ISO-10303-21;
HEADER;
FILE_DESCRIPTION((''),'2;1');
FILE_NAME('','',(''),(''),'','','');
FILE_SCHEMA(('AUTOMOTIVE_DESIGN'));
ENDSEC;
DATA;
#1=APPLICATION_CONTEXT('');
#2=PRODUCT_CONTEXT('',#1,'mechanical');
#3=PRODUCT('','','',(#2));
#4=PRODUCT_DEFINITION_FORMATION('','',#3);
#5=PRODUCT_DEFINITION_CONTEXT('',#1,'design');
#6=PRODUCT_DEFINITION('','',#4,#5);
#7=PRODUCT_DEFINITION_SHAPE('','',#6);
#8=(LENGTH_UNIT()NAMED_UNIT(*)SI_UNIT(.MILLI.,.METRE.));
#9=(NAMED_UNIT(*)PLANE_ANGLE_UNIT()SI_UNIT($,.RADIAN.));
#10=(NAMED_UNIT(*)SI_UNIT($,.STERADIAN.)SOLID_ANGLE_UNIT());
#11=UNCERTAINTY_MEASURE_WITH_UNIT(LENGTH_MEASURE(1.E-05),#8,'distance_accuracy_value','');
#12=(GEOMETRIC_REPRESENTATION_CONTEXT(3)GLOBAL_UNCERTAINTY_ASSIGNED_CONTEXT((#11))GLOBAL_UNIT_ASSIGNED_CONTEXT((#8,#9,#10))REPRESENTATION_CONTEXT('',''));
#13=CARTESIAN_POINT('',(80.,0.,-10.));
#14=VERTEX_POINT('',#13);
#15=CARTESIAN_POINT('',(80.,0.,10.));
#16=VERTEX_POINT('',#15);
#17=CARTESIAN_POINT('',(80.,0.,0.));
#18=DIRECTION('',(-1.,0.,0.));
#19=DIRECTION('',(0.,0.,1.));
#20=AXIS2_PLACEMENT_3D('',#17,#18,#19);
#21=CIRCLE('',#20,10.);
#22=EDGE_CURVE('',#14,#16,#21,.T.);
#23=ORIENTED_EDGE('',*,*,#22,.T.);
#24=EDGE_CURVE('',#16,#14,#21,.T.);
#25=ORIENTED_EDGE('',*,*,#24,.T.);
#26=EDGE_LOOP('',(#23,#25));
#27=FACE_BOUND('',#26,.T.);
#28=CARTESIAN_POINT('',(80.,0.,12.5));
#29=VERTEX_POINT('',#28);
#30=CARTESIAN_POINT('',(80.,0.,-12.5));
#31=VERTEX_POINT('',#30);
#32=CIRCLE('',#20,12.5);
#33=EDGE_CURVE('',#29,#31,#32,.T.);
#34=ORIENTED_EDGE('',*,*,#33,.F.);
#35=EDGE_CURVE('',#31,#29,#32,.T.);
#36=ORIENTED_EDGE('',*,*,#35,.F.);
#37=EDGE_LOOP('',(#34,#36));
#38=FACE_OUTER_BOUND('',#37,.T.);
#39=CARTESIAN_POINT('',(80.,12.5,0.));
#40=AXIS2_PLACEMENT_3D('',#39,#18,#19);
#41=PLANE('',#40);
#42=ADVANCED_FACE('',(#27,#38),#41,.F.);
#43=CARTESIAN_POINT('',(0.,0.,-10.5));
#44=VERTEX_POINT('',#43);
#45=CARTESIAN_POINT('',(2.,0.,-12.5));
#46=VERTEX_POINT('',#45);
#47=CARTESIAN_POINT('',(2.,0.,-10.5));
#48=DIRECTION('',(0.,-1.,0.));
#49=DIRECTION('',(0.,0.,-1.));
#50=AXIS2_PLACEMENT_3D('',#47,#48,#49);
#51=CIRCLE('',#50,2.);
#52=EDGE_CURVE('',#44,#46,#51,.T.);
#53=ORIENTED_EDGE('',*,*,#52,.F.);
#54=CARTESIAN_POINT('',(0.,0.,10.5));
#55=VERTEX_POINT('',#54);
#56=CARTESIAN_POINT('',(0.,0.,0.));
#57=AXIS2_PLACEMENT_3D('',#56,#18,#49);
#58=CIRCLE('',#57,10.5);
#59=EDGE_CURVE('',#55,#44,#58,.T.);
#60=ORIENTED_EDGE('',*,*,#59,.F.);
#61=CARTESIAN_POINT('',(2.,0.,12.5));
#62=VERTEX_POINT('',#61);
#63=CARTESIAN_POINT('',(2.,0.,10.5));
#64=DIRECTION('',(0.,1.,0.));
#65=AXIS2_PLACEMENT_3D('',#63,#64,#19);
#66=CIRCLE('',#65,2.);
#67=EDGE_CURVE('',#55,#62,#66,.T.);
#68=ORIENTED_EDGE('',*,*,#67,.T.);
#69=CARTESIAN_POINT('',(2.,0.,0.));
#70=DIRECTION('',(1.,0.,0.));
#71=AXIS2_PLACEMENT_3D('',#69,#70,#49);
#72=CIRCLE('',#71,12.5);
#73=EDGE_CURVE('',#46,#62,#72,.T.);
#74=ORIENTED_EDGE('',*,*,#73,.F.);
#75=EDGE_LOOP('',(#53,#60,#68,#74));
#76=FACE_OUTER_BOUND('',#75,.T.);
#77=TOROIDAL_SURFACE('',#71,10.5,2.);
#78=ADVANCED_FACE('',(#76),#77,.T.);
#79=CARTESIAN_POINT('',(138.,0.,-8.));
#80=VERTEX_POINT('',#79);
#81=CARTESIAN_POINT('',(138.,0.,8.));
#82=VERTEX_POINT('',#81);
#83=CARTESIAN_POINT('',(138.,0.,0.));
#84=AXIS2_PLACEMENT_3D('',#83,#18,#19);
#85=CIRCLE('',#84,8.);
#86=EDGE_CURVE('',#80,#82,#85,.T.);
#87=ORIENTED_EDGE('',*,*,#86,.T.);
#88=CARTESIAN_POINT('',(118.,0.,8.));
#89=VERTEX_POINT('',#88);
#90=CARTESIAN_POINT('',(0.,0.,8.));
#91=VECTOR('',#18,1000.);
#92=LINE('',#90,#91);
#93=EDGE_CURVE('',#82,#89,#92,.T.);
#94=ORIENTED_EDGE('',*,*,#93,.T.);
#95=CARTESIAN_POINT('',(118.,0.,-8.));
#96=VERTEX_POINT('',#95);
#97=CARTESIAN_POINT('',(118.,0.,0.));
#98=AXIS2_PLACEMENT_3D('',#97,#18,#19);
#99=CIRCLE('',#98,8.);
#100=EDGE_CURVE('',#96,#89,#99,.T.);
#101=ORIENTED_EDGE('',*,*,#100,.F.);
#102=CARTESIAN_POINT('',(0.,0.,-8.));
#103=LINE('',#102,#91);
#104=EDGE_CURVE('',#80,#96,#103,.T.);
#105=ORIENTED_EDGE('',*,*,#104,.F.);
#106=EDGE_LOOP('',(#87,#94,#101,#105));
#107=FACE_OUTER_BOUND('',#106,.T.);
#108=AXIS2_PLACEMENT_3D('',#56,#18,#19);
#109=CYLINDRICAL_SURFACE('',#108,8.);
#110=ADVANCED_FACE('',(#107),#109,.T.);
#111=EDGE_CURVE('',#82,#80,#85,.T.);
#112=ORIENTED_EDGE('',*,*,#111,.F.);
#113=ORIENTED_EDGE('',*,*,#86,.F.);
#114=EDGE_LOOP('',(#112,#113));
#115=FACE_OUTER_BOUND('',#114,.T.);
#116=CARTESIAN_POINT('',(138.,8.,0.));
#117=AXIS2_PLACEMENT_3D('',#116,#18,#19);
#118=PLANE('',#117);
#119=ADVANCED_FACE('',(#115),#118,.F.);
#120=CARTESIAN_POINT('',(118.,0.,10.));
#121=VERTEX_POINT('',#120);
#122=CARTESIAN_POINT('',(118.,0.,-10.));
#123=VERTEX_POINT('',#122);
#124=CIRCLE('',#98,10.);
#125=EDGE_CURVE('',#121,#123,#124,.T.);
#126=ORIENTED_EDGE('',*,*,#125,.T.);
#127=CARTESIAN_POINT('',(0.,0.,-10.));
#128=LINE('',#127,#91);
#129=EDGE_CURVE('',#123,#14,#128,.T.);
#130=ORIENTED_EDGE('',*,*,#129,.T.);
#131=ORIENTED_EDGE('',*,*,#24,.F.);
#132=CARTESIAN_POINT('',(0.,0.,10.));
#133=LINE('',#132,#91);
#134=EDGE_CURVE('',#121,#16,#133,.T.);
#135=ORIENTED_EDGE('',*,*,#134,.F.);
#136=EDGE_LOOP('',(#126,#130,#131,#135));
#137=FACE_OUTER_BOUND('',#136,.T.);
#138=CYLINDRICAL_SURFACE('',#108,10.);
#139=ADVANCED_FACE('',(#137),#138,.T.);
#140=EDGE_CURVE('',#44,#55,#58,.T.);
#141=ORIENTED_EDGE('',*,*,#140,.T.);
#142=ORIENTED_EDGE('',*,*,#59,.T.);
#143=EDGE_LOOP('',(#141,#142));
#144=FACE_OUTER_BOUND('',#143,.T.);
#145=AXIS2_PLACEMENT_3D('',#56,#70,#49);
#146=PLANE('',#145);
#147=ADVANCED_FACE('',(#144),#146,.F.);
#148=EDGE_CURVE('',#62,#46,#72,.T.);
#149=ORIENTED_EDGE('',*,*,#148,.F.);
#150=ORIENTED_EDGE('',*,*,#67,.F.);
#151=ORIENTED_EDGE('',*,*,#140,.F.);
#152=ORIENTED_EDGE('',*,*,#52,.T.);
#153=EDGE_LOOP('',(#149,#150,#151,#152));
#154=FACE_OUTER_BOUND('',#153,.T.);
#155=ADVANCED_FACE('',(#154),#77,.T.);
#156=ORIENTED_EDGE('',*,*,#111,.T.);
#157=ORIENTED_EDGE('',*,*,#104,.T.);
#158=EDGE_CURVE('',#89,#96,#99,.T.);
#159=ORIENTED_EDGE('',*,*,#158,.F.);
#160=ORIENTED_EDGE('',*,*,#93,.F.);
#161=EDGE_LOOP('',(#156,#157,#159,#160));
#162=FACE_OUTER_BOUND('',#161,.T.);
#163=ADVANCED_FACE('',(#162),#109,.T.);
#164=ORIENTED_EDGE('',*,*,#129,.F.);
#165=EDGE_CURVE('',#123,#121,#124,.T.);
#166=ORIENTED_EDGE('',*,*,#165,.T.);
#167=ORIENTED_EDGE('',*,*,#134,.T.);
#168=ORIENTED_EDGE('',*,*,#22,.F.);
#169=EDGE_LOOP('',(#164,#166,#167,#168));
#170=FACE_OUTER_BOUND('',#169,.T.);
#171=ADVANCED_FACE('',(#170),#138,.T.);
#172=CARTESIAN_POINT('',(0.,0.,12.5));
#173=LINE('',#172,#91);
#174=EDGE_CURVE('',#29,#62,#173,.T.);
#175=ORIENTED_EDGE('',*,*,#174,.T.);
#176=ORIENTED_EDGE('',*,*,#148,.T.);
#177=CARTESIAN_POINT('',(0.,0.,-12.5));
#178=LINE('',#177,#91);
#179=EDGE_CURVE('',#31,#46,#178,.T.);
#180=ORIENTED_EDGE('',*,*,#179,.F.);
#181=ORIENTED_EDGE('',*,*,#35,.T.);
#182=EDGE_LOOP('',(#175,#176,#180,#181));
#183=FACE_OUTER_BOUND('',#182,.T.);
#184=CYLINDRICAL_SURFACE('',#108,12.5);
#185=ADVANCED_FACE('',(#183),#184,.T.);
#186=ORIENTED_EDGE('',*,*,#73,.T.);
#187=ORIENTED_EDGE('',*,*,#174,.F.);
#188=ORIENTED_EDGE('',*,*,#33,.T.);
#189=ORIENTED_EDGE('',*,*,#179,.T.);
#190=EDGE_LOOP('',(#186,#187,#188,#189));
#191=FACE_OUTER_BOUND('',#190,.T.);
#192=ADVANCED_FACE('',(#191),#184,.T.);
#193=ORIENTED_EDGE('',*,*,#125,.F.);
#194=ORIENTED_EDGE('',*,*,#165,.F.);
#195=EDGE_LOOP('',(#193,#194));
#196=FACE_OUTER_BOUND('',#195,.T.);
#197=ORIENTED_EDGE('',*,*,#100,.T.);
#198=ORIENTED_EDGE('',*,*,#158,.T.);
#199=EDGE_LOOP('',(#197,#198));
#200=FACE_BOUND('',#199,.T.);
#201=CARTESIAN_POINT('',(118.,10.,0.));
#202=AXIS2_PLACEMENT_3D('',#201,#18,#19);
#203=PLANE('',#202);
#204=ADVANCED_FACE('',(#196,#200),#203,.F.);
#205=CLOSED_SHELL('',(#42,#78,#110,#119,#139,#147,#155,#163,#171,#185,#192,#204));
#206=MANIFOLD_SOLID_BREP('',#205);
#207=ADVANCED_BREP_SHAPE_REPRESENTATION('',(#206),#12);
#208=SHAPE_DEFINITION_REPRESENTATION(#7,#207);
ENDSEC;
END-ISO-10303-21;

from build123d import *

# Parameters (mm, degrees)
FILLET1_R = 2


with BuildPart() as part:
    # Sketch3 → Revolve1 (revolve)
    with BuildSketch(Plane.XY, mode=Mode.PRIVATE) as revolve1_sk:
        Polygon((0, 0), (0, 12.5), (80, 12.5), (80, 10), (118, 10), (118, 8), (138, 8), (138, 0), align=None)
    revolve(revolve1_sk.sketch.rotate(Axis((0, 0, 0), (1, 0, 0)), 90), axis=Axis((0, 0, 0), (1, 0, 0)))

    # Fillet1
    fillet1_edges = [part.edges().sort_by_distance(p)[0] for p in [
        (0, 0, -12.5),
    ]]
    fillet(fillet1_edges, radius=FILLET1_R)


solid = part.part
